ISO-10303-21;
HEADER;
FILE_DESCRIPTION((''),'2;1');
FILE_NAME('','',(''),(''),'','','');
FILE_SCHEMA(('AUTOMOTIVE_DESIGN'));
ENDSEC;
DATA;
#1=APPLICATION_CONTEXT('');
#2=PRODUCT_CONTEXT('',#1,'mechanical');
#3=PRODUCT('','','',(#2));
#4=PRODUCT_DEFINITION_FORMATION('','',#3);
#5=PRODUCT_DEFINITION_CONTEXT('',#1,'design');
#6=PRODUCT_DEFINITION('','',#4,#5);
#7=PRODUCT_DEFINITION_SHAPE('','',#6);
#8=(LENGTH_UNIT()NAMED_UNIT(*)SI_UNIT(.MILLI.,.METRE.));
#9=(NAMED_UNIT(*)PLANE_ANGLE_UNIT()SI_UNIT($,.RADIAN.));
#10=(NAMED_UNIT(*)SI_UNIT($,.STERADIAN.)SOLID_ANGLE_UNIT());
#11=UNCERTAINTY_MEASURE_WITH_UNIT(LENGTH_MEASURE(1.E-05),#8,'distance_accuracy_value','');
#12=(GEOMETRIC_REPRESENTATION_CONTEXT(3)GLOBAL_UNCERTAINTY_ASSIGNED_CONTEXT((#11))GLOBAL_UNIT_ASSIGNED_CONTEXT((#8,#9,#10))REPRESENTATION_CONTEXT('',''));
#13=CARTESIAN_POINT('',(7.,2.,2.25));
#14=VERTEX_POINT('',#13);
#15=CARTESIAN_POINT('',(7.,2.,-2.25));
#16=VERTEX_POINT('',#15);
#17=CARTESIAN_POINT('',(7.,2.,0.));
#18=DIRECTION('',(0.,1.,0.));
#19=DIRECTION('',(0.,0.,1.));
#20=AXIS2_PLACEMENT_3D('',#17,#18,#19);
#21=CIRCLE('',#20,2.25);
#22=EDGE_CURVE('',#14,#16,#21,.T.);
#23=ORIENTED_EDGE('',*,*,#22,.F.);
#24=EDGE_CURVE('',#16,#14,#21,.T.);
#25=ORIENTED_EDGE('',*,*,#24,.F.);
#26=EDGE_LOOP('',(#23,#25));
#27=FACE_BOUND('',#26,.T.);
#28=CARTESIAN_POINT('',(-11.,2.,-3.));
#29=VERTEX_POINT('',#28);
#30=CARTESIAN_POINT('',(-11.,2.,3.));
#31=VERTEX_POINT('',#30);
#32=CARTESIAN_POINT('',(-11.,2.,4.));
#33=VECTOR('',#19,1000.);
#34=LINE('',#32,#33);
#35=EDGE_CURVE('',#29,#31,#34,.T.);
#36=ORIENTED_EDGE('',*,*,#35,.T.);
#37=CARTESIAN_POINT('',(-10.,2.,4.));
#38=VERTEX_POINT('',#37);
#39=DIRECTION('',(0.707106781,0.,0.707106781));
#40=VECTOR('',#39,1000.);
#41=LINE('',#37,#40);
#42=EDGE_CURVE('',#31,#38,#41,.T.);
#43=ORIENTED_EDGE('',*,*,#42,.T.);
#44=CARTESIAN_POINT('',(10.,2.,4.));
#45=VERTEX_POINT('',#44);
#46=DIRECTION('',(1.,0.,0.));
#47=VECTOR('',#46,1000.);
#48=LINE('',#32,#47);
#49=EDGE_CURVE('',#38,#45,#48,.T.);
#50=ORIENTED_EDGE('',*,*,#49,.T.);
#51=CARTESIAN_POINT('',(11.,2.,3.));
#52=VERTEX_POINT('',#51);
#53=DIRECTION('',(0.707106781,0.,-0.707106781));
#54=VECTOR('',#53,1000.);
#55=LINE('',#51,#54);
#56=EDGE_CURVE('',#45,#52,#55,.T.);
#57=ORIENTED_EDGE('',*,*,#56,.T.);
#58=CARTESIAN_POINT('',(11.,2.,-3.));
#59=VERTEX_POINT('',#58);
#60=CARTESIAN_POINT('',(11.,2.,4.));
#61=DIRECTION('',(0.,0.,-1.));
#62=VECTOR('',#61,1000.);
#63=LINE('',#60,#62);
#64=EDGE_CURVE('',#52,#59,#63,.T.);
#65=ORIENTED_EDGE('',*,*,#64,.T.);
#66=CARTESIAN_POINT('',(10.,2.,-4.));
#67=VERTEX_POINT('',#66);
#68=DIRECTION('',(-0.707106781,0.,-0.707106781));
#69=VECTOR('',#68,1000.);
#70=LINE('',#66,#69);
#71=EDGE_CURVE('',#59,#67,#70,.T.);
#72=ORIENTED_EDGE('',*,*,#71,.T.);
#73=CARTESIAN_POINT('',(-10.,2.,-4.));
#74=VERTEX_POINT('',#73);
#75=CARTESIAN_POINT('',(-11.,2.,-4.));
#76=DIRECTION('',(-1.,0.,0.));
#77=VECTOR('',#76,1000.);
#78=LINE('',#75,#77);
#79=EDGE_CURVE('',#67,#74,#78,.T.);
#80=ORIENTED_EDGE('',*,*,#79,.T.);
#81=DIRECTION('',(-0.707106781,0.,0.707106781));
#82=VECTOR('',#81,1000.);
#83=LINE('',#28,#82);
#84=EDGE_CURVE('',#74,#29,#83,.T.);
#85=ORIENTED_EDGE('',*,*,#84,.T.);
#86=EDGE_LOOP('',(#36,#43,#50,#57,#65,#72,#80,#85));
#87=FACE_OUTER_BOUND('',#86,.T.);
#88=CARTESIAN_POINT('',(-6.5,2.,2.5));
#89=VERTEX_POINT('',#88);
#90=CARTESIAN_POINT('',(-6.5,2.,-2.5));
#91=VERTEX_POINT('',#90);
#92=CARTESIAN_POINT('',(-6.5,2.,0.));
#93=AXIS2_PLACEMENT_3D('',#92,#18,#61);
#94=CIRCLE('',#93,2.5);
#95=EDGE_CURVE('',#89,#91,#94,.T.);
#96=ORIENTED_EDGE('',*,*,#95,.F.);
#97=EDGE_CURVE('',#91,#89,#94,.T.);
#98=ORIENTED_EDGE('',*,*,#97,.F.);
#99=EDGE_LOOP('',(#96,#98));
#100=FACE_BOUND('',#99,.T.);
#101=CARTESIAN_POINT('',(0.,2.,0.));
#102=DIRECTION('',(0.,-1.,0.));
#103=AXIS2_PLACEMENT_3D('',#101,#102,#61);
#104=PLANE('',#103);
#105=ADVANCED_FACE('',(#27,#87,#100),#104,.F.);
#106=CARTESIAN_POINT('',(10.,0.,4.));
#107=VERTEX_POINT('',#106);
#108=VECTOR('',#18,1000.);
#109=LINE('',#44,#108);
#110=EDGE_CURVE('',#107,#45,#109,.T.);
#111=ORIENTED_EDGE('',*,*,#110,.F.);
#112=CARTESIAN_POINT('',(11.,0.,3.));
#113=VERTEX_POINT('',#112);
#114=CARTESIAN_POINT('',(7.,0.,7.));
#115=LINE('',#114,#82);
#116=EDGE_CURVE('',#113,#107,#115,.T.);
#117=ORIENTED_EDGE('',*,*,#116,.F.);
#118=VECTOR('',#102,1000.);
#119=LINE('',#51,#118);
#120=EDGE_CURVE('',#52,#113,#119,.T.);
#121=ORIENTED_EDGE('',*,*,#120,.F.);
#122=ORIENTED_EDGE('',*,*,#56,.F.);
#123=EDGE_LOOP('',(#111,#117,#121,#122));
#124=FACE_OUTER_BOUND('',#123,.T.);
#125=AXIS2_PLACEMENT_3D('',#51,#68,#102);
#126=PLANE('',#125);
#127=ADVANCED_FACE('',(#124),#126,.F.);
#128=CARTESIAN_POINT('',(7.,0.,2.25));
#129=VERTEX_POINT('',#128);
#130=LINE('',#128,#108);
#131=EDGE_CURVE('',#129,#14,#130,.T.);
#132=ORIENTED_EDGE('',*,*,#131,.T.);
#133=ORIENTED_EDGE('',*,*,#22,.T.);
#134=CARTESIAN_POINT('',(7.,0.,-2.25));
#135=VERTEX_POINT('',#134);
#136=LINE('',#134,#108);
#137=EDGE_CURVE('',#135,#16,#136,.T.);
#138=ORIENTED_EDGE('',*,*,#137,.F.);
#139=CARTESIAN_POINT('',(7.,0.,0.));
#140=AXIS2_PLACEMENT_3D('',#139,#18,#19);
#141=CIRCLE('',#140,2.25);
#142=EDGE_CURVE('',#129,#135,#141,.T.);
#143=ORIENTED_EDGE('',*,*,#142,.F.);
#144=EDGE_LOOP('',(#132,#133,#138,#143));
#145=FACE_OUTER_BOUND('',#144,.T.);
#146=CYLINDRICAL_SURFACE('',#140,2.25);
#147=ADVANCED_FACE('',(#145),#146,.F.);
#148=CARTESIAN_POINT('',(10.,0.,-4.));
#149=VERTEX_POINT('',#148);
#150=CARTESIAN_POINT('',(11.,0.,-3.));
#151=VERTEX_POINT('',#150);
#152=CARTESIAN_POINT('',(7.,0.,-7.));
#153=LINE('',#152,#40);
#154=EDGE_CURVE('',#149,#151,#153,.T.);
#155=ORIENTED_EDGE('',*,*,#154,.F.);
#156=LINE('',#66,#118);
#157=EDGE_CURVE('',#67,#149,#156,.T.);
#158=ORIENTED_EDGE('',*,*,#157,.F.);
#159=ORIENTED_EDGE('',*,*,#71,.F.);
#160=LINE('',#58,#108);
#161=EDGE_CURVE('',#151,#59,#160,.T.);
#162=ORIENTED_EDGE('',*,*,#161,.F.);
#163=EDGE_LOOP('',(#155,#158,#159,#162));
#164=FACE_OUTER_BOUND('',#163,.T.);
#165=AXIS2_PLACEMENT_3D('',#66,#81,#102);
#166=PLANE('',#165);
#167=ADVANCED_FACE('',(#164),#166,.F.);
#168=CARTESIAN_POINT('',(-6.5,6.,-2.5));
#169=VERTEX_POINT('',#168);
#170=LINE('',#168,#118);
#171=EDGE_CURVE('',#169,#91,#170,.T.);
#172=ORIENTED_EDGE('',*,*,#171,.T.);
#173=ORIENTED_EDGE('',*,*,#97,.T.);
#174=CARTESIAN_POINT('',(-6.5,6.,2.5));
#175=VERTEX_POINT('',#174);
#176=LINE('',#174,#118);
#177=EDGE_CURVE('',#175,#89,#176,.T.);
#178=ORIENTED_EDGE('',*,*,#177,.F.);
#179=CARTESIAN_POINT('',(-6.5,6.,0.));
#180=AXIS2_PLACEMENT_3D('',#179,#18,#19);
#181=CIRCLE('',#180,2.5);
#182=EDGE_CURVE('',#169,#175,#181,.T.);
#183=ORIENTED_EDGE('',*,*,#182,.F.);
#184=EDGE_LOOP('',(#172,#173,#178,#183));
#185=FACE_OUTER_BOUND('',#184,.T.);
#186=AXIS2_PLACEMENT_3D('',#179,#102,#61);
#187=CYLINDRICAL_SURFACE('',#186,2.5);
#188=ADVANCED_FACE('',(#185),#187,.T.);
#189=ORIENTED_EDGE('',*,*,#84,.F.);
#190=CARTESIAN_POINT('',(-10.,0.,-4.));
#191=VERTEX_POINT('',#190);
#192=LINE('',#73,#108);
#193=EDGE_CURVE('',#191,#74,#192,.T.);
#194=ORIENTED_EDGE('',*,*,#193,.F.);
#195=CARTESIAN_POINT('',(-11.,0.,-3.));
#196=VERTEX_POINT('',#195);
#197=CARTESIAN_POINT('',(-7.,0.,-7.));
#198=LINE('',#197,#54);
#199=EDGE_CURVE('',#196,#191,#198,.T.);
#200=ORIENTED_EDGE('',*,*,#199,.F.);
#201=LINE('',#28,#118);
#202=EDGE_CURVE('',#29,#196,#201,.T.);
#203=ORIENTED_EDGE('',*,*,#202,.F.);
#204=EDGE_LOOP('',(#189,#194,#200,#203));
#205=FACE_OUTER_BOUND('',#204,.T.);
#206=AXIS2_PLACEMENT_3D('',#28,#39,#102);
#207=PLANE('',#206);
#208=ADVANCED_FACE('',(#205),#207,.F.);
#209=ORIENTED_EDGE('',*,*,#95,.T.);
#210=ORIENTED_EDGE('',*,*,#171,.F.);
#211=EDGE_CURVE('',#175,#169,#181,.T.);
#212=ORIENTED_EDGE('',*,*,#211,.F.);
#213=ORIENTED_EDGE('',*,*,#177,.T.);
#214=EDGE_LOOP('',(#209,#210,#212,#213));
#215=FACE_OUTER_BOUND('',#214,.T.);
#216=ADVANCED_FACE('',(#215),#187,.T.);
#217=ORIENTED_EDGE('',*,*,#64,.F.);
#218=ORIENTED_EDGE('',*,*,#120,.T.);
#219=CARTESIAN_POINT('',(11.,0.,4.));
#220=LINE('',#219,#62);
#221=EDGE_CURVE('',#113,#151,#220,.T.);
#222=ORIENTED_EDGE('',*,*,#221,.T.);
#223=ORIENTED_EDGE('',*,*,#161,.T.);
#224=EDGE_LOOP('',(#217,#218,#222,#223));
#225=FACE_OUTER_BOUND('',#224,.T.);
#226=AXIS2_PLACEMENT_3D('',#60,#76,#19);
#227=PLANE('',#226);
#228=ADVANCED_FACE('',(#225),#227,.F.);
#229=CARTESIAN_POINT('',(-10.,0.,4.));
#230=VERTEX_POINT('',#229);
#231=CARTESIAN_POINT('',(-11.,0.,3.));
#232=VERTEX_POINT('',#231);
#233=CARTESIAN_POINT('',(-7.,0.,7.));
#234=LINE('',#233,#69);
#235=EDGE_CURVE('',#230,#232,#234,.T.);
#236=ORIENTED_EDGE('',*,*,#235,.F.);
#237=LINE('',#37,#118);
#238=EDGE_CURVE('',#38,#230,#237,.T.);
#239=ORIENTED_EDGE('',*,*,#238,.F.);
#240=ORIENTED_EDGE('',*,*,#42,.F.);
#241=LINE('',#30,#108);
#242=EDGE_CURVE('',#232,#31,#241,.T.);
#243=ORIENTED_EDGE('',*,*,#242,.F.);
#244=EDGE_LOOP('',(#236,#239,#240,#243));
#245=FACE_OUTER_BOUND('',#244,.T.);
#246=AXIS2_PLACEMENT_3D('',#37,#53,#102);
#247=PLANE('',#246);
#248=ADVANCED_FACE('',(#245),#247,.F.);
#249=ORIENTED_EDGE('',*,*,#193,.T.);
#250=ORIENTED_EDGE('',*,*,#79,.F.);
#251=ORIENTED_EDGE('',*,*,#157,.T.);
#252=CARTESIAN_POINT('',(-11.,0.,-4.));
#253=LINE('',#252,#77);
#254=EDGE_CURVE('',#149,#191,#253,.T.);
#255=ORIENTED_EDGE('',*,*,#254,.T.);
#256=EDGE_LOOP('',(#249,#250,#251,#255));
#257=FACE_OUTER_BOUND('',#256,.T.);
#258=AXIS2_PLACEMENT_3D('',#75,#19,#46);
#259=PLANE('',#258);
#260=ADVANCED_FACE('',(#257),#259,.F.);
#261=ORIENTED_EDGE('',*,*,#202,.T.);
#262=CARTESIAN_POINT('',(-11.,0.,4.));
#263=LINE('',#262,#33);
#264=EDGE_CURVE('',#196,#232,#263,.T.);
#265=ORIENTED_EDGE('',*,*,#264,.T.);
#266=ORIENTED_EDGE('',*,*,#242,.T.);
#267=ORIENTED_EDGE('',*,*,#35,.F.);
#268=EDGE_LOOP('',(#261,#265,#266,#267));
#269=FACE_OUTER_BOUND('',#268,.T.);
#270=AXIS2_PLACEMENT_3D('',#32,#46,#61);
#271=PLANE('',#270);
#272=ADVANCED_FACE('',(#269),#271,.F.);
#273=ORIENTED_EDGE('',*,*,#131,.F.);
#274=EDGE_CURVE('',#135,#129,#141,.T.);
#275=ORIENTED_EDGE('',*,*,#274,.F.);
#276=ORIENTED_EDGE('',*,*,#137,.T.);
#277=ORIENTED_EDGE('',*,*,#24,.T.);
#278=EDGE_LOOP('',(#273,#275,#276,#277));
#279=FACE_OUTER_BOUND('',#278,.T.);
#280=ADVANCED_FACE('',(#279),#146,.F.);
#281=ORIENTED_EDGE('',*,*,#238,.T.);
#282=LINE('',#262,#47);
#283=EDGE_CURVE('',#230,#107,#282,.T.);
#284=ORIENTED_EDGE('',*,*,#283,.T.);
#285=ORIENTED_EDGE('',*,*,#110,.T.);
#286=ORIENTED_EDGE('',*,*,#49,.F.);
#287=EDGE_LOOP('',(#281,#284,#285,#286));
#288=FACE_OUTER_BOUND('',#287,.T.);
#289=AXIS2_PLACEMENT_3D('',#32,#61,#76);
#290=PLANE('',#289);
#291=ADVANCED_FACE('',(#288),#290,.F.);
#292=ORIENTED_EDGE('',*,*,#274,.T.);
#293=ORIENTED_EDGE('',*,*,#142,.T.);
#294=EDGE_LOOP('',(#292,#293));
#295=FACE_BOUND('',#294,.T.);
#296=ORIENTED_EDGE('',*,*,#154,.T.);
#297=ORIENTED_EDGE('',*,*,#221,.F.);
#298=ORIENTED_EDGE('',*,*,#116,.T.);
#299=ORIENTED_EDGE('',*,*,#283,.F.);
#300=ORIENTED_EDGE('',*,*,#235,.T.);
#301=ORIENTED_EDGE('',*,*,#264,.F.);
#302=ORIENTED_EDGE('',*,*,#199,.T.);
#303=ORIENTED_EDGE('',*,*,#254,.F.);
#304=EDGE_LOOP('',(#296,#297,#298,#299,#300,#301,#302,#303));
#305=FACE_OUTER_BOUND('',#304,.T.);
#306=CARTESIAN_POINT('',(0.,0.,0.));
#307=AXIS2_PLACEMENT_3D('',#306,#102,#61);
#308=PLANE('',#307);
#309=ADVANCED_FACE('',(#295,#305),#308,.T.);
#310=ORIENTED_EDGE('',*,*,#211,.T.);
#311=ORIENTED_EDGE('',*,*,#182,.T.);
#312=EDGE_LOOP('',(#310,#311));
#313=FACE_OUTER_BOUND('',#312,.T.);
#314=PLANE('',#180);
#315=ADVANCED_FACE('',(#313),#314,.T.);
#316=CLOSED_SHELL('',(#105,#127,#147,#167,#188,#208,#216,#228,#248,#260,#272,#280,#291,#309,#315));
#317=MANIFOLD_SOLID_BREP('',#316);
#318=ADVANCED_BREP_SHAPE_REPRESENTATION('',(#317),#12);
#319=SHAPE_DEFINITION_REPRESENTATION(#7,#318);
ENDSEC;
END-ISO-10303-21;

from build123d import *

# Parameters (mm, degrees)
SKETCH1_W           = 22
SKETCH1_H           = 8
BOSS_EXTRUDE1_DEPTH = 2
SKETCH2_R           = 2.25
CUT_EXTRUDE1_DEPTH  = 12.874342087
SKETCH3_R           = 2.5
BOSS_EXTRUDE2_DEPTH = 4
CHAMFER1_SIZE       = 1


with BuildPart() as part:
    # Sketch1 → Boss-Extrude1 (new body)
    with BuildSketch(Plane(origin=(0, 0, 0), x_dir=(1, 0, 0), z_dir=(0, 1, 0))):
        Rectangle(SKETCH1_W, SKETCH1_H)
    extrude(amount=BOSS_EXTRUDE1_DEPTH)

    # Sketch2 → Cut-Extrude1 (cut, through all)
    with BuildSketch(Plane(origin=(0, 2, 0), x_dir=(1, 0, 0), z_dir=(0, 1, 0))):
        with Locations(Location((7, 0, 0), (0, 0, 270))):
            Circle(SKETCH2_R)
    extrude(amount=-CUT_EXTRUDE1_DEPTH, mode=Mode.SUBTRACT)

    # Sketch3 → Boss-Extrude2 (add)
    with BuildSketch(Plane(origin=(0, 2, 0), x_dir=(1, 0, 0), z_dir=(0, 1, 0))):
        with Locations(Location((-6.5, 0, 0), (0, 0, 90))):
            Circle(SKETCH3_R)
    extrude(amount=BOSS_EXTRUDE2_DEPTH)

    # Chamfer1
    chamfer1_edges = [part.edges().sort_by_distance(p)[0] for p in [
        (11, 1, 4),
        (-11, 1, 4),
        (-11, 1, -4),
        (11, 1, -4),
    ]]
    chamfer(chamfer1_edges, length=CHAMFER1_SIZE)


solid = part.part
